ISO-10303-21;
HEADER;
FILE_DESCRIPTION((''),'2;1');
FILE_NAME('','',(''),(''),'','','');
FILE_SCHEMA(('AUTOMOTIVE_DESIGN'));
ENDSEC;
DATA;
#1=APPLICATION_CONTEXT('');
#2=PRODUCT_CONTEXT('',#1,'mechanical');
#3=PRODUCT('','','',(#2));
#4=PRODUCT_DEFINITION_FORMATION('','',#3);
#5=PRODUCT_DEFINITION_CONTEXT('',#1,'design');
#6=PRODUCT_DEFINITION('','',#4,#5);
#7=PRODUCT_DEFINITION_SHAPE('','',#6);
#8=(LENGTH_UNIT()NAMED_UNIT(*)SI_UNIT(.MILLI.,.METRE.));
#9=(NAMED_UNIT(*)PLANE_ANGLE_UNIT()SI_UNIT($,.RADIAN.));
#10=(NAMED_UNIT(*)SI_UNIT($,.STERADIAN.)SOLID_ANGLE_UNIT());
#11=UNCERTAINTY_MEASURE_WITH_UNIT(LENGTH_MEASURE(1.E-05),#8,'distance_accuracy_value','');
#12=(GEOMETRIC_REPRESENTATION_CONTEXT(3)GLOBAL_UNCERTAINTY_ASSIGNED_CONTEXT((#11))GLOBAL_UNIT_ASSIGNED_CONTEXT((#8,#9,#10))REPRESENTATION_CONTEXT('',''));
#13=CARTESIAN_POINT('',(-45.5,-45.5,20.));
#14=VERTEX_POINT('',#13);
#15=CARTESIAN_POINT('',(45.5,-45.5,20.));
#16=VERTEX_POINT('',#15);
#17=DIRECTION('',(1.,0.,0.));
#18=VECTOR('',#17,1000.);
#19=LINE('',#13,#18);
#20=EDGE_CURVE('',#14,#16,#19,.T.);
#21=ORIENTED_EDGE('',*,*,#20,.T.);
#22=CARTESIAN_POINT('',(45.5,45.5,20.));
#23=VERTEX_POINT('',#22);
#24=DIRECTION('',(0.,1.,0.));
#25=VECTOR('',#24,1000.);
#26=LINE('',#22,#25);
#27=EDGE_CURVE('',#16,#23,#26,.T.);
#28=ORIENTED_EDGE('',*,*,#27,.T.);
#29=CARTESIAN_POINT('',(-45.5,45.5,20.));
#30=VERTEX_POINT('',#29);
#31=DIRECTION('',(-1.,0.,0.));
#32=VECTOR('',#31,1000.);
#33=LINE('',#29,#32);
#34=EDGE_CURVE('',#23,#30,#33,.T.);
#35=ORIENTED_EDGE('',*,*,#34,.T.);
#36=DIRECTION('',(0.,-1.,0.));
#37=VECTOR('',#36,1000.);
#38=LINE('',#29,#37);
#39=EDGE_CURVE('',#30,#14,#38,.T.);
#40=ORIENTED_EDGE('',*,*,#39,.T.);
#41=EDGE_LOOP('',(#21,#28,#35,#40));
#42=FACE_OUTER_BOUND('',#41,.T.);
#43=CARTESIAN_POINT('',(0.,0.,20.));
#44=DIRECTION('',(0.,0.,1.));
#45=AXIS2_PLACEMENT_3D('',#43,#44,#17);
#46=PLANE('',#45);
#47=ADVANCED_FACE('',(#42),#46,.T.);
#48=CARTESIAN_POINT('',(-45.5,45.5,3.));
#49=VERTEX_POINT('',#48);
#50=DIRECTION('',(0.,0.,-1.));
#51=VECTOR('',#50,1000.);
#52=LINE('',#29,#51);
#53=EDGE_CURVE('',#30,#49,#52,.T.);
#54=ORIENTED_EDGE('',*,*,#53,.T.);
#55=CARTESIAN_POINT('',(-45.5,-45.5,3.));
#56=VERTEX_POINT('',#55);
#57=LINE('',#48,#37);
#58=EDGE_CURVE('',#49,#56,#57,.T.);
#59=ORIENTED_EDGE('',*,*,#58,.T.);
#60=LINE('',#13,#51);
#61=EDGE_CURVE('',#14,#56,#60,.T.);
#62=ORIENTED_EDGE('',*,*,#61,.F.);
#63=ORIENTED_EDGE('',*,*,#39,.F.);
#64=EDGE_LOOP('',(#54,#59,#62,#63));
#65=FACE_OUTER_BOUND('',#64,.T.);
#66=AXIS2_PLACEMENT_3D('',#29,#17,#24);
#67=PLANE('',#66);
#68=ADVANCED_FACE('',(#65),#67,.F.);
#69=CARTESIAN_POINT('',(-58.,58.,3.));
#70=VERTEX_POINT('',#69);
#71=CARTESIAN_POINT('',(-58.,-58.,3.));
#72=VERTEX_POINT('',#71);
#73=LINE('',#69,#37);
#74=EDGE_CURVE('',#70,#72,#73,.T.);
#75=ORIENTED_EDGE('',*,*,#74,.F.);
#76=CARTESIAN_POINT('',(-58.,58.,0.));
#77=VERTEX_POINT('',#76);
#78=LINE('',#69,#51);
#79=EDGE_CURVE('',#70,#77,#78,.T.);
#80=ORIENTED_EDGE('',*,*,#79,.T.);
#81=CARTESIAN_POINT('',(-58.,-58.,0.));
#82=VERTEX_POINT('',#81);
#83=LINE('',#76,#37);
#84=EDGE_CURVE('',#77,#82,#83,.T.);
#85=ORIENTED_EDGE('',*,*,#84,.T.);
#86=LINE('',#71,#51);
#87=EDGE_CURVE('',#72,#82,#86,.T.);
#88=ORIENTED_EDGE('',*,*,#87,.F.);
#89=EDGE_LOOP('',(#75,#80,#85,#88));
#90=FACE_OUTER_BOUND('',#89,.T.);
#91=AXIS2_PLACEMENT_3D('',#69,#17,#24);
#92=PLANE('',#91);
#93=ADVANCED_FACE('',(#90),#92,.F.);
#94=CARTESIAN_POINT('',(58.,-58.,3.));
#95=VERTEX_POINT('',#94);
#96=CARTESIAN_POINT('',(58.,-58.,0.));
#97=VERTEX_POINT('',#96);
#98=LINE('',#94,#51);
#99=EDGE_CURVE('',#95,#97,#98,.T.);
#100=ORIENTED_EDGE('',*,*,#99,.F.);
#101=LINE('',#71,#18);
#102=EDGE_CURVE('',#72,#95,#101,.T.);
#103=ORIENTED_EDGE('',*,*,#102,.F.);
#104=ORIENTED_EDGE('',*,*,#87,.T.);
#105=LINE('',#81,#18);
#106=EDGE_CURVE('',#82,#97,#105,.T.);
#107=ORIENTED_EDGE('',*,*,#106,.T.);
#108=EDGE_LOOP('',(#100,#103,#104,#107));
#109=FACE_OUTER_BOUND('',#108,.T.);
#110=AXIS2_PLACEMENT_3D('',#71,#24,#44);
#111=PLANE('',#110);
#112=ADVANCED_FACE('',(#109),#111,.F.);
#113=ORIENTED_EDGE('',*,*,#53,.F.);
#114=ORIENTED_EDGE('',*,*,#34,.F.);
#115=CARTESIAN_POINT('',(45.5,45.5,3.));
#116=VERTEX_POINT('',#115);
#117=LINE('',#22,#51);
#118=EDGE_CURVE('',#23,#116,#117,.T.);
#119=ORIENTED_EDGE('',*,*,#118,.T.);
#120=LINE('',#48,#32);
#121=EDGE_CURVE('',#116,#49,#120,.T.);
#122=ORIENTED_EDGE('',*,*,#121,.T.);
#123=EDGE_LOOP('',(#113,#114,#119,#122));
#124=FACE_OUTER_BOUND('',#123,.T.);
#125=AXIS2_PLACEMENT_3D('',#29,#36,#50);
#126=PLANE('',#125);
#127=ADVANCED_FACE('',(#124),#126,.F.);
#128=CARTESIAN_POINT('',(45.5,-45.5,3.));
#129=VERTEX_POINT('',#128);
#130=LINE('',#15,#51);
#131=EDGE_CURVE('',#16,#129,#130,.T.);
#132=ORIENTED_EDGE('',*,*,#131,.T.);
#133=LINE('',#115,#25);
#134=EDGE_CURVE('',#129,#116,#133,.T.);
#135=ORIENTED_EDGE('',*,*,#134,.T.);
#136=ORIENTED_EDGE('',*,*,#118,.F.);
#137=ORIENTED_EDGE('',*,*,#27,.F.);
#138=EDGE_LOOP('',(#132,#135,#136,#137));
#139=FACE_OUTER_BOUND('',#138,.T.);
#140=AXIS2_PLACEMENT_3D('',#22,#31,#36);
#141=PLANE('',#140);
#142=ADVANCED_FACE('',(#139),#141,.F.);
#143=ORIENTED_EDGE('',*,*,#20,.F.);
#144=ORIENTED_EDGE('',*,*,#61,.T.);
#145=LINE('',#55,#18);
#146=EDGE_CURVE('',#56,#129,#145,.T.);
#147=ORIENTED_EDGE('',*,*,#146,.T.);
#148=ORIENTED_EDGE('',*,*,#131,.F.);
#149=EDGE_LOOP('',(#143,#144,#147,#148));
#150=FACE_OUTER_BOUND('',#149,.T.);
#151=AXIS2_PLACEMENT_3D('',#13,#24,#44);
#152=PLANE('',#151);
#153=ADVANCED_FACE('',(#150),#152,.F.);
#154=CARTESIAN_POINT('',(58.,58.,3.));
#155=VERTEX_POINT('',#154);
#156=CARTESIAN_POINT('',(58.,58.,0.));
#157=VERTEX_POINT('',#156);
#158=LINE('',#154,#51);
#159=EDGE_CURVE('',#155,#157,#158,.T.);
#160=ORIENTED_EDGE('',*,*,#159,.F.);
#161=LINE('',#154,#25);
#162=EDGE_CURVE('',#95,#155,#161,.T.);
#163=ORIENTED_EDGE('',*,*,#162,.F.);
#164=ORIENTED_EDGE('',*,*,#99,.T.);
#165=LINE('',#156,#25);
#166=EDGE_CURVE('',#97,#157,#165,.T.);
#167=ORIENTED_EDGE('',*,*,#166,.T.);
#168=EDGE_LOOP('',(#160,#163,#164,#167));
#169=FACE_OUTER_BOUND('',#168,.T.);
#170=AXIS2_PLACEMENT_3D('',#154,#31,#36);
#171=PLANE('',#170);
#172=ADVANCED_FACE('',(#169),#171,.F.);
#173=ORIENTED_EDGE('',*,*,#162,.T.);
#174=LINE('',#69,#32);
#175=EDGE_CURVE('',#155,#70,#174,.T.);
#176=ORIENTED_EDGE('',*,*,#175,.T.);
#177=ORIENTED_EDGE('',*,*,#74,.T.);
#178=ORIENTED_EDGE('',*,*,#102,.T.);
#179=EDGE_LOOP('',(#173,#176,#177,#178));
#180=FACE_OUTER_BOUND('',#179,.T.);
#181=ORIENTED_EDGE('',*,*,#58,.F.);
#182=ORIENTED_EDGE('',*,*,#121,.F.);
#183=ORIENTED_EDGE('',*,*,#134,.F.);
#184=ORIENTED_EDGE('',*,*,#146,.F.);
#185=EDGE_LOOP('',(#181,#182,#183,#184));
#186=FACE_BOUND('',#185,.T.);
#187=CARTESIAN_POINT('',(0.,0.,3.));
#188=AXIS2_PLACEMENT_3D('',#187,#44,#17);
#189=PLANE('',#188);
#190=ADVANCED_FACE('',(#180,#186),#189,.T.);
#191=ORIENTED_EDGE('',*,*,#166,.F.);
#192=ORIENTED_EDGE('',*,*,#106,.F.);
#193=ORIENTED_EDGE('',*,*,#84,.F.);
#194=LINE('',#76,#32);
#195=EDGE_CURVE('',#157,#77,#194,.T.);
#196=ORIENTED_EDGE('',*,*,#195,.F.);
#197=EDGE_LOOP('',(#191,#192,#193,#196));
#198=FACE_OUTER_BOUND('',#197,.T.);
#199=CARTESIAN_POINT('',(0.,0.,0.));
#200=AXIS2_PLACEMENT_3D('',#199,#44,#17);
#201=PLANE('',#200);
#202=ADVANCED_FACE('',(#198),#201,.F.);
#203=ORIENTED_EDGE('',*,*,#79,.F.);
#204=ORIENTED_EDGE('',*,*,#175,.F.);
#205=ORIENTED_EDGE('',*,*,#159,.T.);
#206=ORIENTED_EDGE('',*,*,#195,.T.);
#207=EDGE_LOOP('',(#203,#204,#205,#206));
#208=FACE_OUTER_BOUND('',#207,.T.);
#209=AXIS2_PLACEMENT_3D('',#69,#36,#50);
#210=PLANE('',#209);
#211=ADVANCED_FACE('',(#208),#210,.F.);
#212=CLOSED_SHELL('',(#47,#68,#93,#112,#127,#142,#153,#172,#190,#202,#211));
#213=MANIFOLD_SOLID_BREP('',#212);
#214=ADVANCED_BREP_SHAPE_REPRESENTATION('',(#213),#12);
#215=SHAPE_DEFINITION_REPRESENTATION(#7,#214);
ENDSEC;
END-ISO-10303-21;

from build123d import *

# Parameters (mm, degrees)
SKETCH_1_W      = 116
SKETCH_1_H      = 116
EXTRUDE_1_DEPTH = 3
SKETCH_2_W      = 91
SKETCH_2_H      = 91
EXTRUDE_2_DEPTH = 17


with BuildPart() as part:
    # 草图1 → 凸台-拉伸1 (new body)
    with BuildSketch(Plane.XY):
        Rectangle(SKETCH_1_W, SKETCH_1_H)
    extrude(amount=EXTRUDE_1_DEPTH)

    # 草图2 → 凸台-拉伸2 (add)
    with BuildSketch(Plane.XY.offset(3)):
        Rectangle(SKETCH_2_W, SKETCH_2_H)
    extrude(amount=EXTRUDE_2_DEPTH)


solid = part.part
